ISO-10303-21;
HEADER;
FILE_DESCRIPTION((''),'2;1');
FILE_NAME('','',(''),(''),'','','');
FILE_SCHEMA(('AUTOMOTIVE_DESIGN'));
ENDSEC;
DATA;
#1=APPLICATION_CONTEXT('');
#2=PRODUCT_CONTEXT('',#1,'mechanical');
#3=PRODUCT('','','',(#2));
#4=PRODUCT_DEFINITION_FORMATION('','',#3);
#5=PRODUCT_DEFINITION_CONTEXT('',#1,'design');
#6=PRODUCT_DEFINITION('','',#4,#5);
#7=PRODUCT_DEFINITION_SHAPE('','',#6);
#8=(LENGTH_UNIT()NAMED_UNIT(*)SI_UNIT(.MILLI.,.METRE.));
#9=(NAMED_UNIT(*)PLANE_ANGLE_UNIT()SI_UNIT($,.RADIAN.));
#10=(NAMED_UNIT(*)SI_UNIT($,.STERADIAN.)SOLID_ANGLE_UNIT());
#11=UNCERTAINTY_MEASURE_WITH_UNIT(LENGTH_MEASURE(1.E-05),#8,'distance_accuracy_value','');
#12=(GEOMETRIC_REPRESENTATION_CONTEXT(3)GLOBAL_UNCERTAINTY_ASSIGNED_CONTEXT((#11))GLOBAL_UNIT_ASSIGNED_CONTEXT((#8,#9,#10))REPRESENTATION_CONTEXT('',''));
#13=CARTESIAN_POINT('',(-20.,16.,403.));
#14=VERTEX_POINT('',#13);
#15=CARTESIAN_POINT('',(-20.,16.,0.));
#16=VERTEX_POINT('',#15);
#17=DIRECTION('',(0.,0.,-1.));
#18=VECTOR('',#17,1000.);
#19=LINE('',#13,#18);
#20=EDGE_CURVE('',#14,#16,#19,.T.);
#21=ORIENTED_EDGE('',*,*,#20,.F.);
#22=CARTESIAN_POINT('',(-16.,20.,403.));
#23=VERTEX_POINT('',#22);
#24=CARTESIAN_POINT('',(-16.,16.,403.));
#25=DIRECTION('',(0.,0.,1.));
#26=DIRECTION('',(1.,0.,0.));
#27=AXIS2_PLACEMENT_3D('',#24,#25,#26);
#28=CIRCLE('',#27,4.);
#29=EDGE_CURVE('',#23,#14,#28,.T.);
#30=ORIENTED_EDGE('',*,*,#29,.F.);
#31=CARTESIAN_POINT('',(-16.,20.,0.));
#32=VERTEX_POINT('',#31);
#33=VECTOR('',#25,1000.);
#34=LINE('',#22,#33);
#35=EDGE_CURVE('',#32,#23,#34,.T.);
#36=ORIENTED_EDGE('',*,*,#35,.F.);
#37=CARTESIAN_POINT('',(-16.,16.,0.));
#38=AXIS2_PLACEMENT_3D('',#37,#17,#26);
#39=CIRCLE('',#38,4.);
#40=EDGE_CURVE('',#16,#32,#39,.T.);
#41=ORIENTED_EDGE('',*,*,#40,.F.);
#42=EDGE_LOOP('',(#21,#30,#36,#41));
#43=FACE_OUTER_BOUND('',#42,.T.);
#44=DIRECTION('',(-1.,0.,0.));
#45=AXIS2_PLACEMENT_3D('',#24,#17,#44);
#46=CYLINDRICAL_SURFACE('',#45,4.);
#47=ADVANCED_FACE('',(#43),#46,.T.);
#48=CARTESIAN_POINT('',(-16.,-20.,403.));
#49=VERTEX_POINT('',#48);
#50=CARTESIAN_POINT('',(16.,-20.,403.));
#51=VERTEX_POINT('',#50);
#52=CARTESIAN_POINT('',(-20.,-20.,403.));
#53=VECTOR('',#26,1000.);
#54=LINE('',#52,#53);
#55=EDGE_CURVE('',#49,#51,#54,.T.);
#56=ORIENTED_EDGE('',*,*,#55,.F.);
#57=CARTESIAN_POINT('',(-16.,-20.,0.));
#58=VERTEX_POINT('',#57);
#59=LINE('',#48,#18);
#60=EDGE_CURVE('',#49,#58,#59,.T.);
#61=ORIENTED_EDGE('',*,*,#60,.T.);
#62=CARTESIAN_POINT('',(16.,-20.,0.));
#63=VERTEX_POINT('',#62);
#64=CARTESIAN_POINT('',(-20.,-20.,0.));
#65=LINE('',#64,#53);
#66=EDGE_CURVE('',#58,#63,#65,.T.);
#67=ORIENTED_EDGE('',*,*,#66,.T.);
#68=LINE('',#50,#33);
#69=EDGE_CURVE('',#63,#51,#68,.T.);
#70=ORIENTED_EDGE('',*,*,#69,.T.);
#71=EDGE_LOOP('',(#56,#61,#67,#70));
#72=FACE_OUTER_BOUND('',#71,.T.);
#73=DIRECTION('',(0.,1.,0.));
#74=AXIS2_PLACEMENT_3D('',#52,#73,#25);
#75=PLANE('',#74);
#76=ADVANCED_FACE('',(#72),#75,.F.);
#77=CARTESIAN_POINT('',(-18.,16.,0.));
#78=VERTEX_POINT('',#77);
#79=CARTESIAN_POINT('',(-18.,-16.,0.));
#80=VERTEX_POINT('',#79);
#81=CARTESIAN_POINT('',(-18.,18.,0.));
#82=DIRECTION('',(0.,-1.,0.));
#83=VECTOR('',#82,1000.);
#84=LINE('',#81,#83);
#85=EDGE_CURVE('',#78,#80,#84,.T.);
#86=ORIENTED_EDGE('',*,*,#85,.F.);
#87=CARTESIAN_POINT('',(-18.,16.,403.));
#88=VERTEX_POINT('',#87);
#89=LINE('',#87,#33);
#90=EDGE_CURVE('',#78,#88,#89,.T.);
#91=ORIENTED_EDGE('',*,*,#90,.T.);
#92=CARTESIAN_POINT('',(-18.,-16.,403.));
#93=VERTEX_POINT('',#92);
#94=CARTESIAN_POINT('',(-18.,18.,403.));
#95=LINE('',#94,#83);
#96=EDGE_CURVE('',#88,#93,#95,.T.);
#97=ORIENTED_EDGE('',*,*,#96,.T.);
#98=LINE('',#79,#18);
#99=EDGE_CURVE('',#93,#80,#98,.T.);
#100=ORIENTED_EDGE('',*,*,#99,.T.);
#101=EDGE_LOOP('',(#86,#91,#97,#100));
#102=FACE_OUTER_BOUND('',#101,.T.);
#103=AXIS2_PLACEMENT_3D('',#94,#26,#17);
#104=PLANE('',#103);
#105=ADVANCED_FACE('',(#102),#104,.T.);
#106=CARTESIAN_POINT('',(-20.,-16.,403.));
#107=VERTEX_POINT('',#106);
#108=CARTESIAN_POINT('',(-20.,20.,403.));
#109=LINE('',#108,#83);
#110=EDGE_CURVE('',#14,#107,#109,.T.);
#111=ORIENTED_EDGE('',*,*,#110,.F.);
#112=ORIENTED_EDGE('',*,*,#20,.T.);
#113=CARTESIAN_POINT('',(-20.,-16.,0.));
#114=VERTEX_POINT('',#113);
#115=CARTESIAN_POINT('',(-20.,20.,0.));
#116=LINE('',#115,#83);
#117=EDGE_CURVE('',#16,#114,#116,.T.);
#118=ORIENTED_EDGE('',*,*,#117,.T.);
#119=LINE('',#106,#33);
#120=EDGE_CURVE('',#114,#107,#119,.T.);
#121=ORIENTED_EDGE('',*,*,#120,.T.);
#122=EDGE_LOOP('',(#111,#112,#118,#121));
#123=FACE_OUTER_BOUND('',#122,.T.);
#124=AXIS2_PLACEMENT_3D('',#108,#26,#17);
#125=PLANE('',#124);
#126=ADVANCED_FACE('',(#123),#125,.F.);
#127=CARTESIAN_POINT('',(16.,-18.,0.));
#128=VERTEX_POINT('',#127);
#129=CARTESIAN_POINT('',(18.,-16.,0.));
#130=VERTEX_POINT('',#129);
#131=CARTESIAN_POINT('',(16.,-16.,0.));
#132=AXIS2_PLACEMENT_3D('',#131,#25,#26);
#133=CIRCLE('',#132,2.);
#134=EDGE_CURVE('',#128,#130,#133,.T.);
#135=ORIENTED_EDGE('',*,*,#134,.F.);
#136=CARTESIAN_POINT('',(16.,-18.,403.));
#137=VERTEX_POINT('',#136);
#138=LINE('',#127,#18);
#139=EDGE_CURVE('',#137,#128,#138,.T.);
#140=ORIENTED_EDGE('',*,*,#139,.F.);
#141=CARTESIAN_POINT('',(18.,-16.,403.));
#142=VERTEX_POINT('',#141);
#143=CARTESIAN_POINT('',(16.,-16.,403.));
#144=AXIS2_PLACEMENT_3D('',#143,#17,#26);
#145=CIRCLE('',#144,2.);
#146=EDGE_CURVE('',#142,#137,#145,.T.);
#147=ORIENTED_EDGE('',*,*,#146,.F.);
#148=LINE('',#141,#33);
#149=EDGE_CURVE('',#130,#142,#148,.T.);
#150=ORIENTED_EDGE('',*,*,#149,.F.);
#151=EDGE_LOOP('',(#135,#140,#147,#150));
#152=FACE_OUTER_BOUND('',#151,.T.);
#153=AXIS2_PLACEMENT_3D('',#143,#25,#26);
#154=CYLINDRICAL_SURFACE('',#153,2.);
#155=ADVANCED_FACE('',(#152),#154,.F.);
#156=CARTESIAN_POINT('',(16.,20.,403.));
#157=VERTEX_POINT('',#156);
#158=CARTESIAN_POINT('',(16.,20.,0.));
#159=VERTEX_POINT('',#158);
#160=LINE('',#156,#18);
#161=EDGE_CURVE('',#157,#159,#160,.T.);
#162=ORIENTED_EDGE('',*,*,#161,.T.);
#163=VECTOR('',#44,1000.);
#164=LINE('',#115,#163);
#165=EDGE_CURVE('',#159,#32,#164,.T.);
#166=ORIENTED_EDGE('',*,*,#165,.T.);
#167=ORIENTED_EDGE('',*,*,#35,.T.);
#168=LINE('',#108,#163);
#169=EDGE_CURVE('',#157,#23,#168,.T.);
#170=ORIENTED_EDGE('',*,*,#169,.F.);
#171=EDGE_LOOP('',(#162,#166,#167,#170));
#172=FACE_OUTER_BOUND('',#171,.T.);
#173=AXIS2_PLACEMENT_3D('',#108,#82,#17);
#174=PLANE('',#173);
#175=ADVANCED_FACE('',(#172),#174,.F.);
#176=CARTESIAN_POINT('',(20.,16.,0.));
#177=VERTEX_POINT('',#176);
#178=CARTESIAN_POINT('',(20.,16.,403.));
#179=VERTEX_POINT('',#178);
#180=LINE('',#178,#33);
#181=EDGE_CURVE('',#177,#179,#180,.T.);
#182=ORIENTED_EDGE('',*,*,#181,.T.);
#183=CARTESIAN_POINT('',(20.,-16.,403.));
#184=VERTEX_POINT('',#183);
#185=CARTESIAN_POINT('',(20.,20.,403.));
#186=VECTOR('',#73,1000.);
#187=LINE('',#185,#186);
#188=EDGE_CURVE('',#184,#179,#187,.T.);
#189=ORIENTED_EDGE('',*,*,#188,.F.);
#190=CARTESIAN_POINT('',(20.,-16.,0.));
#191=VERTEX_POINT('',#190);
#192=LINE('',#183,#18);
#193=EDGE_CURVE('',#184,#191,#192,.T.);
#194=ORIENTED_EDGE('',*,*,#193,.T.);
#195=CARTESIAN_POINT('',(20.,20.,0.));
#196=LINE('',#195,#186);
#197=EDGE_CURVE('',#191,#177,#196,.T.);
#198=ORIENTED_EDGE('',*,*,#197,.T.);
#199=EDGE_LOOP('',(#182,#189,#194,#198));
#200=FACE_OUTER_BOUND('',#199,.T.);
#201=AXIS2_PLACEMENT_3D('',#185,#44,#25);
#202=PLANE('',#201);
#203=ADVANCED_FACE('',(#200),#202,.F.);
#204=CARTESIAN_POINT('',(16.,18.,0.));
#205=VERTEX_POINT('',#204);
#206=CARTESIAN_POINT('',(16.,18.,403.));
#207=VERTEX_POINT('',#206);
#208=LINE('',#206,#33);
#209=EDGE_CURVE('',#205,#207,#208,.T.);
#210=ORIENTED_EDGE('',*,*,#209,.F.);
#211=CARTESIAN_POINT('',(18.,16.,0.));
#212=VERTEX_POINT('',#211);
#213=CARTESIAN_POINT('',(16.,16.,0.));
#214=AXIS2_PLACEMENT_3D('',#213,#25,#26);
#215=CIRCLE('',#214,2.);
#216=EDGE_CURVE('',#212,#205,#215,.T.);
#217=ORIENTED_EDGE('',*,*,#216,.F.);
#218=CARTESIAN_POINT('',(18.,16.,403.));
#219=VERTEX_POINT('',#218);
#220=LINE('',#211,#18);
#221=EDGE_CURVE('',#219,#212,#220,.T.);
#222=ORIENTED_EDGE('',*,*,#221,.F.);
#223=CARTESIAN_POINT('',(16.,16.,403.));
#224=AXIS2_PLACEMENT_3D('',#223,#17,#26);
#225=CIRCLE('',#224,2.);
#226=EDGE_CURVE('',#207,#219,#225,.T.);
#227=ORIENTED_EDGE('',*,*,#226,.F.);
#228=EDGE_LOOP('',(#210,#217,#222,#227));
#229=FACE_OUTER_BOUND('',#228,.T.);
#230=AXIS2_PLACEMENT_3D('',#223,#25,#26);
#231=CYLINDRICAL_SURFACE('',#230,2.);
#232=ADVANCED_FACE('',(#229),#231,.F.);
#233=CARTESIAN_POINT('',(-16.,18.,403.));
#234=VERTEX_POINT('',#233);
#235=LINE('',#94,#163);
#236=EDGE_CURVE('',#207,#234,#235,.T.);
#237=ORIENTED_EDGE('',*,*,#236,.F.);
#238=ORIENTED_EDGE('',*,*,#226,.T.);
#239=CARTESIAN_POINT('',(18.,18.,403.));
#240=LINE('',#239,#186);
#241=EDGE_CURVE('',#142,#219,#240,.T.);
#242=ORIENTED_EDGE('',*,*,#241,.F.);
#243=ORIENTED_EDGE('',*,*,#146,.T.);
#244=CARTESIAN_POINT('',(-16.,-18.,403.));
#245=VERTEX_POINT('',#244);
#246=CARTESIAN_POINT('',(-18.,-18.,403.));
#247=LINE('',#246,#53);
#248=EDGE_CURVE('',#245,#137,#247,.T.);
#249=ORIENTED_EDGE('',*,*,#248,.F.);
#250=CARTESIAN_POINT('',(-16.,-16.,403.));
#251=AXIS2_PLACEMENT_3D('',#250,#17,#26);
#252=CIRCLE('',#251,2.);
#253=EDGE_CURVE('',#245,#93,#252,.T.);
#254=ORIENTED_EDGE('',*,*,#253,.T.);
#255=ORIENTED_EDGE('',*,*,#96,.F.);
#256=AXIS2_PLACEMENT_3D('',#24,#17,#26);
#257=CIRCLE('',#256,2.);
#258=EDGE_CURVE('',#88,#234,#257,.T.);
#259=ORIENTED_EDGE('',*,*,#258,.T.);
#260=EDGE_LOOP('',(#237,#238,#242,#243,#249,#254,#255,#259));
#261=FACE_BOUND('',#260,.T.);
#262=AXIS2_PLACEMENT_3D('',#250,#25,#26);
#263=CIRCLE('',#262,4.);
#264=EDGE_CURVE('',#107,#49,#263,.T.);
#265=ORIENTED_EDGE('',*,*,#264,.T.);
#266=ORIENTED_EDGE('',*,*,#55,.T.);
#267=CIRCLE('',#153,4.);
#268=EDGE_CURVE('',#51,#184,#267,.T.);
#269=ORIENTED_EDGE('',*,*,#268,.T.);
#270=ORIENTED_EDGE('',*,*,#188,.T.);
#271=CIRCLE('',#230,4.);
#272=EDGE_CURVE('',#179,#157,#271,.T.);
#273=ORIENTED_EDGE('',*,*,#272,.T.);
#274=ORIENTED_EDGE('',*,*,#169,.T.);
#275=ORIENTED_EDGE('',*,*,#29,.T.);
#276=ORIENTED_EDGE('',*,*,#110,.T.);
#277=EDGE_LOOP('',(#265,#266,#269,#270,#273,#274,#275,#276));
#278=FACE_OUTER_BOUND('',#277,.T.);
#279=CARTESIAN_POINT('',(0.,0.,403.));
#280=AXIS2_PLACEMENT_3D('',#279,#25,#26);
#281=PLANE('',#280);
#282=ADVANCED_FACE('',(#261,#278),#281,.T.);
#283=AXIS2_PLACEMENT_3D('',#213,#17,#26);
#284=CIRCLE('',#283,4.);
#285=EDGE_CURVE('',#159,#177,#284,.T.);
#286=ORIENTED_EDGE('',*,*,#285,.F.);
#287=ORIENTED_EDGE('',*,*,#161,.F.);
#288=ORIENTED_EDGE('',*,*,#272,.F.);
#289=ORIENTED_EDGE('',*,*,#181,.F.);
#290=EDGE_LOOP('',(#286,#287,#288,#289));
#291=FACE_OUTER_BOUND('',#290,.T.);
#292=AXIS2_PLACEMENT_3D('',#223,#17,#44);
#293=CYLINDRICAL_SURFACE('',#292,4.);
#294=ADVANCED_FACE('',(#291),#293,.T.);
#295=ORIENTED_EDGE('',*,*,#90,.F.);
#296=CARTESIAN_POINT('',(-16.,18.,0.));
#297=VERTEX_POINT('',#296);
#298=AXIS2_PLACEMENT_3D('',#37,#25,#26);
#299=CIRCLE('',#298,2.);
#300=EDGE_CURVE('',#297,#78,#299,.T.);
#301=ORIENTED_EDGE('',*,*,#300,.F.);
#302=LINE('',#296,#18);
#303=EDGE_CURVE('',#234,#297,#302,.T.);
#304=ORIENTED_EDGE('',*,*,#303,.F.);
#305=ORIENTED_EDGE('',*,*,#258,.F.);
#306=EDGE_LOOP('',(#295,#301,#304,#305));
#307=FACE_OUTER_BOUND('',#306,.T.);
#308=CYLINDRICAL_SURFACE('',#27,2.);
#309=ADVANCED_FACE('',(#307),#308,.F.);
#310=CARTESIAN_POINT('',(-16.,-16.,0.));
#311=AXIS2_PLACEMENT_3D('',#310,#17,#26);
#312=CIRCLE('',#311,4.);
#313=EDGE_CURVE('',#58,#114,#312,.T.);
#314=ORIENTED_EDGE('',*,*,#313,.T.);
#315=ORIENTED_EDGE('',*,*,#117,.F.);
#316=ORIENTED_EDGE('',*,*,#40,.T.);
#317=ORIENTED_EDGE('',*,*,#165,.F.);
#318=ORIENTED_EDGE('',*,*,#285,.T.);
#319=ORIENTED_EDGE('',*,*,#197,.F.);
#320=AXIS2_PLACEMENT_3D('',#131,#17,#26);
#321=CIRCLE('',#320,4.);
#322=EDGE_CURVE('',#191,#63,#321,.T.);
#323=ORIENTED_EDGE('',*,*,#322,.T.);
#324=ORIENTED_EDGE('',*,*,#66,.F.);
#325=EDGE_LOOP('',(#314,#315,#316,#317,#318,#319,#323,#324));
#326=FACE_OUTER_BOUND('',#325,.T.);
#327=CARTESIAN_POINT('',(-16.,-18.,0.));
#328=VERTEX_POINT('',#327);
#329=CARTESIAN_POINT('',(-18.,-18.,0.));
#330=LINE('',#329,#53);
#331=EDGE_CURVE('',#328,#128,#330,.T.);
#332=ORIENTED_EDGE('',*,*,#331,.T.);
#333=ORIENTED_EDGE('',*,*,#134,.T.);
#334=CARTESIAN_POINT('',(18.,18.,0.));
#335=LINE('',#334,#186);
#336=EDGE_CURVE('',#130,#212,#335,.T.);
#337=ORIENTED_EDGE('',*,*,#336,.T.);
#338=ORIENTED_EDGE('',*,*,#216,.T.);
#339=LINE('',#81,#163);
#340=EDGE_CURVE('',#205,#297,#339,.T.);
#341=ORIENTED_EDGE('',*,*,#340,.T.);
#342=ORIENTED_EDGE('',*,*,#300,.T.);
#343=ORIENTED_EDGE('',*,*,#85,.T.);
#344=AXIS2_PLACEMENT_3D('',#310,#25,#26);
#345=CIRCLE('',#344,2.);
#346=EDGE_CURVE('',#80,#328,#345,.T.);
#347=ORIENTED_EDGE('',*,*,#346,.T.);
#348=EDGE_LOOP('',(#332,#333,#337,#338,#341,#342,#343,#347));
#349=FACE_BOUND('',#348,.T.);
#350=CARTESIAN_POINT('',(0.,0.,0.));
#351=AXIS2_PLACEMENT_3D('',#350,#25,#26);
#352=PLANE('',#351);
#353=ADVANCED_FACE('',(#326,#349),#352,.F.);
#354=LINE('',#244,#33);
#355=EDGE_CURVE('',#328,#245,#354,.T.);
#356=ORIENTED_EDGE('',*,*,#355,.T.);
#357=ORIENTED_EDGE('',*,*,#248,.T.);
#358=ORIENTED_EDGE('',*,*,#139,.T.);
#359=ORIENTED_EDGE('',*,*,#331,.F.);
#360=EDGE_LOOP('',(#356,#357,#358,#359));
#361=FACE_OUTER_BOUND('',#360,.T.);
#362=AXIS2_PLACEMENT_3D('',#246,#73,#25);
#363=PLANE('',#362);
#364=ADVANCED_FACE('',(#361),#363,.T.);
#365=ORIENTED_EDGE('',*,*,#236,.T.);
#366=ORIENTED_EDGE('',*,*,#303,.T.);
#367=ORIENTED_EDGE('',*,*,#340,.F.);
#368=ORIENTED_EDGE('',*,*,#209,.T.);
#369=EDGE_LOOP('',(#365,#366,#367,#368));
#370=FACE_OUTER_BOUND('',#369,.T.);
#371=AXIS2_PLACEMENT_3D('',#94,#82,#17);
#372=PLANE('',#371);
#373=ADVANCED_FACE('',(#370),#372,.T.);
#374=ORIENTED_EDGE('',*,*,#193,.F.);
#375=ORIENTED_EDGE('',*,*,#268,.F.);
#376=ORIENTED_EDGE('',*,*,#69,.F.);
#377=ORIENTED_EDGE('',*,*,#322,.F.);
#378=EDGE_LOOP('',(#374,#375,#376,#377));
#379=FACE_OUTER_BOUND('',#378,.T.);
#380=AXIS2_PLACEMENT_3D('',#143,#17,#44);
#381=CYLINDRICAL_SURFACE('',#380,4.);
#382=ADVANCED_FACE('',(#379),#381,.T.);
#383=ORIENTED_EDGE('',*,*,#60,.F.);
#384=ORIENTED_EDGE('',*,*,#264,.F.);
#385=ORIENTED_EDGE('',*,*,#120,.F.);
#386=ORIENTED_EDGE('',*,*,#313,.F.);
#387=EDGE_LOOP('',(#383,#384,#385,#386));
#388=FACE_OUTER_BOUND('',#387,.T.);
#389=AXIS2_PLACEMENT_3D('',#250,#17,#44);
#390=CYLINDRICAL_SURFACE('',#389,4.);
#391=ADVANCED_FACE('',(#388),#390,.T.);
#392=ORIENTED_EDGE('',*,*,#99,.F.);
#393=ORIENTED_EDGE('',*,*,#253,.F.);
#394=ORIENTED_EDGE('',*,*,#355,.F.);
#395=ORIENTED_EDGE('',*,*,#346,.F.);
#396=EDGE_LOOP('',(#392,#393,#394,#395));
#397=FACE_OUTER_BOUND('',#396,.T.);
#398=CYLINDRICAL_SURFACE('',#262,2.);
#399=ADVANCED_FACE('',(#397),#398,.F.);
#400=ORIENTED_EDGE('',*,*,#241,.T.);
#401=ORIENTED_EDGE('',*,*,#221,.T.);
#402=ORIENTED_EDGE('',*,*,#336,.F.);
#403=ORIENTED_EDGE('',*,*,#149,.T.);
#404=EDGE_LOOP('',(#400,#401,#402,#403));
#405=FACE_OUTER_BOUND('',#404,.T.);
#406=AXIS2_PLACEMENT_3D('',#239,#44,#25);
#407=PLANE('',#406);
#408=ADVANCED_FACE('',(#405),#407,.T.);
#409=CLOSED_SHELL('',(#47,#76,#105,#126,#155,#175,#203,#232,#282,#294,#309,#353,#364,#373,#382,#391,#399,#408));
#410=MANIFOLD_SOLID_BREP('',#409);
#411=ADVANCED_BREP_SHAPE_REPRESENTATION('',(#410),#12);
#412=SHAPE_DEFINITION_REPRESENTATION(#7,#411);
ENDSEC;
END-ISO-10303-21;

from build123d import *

# Parameters (mm, degrees)
SKETCH1_W           = 40
SKETCH1_H           = 40
SKETCH1_W_2         = 36
SKETCH1_H_2         = 36
BOSS_EXTRUDE1_DEPTH = 403
FILLET1_R           = 2
FILLET2_R           = 4


with BuildPart() as part:
    # Sketch1 → Boss-Extrude1 (new body)
    with BuildSketch(Plane.XY):
        Rectangle(SKETCH1_W, SKETCH1_H)
        Rectangle(SKETCH1_W_2, SKETCH1_H_2, mode=Mode.SUBTRACT)
    extrude(amount=BOSS_EXTRUDE1_DEPTH)

    # Fillet1
    fillet1_edges = [part.edges().sort_by_distance(p)[0] for p in [
        (18, -18, 201.5),
        (18, 18, 201.5),
        (-18, 18, 201.5),
        (-18, -18, 201.5),
    ]]
    fillet(fillet1_edges, radius=FILLET1_R)

    # Fillet2
    fillet2_edges = [part.edges().sort_by_distance(p)[0] for p in [
        (20, -20, 201.5),
        (-20, -20, 201.5),
        (-20, 20, 201.5),
        (20, 20, 201.5),
    ]]
    fillet(fillet2_edges, radius=FILLET2_R)


solid = part.part
